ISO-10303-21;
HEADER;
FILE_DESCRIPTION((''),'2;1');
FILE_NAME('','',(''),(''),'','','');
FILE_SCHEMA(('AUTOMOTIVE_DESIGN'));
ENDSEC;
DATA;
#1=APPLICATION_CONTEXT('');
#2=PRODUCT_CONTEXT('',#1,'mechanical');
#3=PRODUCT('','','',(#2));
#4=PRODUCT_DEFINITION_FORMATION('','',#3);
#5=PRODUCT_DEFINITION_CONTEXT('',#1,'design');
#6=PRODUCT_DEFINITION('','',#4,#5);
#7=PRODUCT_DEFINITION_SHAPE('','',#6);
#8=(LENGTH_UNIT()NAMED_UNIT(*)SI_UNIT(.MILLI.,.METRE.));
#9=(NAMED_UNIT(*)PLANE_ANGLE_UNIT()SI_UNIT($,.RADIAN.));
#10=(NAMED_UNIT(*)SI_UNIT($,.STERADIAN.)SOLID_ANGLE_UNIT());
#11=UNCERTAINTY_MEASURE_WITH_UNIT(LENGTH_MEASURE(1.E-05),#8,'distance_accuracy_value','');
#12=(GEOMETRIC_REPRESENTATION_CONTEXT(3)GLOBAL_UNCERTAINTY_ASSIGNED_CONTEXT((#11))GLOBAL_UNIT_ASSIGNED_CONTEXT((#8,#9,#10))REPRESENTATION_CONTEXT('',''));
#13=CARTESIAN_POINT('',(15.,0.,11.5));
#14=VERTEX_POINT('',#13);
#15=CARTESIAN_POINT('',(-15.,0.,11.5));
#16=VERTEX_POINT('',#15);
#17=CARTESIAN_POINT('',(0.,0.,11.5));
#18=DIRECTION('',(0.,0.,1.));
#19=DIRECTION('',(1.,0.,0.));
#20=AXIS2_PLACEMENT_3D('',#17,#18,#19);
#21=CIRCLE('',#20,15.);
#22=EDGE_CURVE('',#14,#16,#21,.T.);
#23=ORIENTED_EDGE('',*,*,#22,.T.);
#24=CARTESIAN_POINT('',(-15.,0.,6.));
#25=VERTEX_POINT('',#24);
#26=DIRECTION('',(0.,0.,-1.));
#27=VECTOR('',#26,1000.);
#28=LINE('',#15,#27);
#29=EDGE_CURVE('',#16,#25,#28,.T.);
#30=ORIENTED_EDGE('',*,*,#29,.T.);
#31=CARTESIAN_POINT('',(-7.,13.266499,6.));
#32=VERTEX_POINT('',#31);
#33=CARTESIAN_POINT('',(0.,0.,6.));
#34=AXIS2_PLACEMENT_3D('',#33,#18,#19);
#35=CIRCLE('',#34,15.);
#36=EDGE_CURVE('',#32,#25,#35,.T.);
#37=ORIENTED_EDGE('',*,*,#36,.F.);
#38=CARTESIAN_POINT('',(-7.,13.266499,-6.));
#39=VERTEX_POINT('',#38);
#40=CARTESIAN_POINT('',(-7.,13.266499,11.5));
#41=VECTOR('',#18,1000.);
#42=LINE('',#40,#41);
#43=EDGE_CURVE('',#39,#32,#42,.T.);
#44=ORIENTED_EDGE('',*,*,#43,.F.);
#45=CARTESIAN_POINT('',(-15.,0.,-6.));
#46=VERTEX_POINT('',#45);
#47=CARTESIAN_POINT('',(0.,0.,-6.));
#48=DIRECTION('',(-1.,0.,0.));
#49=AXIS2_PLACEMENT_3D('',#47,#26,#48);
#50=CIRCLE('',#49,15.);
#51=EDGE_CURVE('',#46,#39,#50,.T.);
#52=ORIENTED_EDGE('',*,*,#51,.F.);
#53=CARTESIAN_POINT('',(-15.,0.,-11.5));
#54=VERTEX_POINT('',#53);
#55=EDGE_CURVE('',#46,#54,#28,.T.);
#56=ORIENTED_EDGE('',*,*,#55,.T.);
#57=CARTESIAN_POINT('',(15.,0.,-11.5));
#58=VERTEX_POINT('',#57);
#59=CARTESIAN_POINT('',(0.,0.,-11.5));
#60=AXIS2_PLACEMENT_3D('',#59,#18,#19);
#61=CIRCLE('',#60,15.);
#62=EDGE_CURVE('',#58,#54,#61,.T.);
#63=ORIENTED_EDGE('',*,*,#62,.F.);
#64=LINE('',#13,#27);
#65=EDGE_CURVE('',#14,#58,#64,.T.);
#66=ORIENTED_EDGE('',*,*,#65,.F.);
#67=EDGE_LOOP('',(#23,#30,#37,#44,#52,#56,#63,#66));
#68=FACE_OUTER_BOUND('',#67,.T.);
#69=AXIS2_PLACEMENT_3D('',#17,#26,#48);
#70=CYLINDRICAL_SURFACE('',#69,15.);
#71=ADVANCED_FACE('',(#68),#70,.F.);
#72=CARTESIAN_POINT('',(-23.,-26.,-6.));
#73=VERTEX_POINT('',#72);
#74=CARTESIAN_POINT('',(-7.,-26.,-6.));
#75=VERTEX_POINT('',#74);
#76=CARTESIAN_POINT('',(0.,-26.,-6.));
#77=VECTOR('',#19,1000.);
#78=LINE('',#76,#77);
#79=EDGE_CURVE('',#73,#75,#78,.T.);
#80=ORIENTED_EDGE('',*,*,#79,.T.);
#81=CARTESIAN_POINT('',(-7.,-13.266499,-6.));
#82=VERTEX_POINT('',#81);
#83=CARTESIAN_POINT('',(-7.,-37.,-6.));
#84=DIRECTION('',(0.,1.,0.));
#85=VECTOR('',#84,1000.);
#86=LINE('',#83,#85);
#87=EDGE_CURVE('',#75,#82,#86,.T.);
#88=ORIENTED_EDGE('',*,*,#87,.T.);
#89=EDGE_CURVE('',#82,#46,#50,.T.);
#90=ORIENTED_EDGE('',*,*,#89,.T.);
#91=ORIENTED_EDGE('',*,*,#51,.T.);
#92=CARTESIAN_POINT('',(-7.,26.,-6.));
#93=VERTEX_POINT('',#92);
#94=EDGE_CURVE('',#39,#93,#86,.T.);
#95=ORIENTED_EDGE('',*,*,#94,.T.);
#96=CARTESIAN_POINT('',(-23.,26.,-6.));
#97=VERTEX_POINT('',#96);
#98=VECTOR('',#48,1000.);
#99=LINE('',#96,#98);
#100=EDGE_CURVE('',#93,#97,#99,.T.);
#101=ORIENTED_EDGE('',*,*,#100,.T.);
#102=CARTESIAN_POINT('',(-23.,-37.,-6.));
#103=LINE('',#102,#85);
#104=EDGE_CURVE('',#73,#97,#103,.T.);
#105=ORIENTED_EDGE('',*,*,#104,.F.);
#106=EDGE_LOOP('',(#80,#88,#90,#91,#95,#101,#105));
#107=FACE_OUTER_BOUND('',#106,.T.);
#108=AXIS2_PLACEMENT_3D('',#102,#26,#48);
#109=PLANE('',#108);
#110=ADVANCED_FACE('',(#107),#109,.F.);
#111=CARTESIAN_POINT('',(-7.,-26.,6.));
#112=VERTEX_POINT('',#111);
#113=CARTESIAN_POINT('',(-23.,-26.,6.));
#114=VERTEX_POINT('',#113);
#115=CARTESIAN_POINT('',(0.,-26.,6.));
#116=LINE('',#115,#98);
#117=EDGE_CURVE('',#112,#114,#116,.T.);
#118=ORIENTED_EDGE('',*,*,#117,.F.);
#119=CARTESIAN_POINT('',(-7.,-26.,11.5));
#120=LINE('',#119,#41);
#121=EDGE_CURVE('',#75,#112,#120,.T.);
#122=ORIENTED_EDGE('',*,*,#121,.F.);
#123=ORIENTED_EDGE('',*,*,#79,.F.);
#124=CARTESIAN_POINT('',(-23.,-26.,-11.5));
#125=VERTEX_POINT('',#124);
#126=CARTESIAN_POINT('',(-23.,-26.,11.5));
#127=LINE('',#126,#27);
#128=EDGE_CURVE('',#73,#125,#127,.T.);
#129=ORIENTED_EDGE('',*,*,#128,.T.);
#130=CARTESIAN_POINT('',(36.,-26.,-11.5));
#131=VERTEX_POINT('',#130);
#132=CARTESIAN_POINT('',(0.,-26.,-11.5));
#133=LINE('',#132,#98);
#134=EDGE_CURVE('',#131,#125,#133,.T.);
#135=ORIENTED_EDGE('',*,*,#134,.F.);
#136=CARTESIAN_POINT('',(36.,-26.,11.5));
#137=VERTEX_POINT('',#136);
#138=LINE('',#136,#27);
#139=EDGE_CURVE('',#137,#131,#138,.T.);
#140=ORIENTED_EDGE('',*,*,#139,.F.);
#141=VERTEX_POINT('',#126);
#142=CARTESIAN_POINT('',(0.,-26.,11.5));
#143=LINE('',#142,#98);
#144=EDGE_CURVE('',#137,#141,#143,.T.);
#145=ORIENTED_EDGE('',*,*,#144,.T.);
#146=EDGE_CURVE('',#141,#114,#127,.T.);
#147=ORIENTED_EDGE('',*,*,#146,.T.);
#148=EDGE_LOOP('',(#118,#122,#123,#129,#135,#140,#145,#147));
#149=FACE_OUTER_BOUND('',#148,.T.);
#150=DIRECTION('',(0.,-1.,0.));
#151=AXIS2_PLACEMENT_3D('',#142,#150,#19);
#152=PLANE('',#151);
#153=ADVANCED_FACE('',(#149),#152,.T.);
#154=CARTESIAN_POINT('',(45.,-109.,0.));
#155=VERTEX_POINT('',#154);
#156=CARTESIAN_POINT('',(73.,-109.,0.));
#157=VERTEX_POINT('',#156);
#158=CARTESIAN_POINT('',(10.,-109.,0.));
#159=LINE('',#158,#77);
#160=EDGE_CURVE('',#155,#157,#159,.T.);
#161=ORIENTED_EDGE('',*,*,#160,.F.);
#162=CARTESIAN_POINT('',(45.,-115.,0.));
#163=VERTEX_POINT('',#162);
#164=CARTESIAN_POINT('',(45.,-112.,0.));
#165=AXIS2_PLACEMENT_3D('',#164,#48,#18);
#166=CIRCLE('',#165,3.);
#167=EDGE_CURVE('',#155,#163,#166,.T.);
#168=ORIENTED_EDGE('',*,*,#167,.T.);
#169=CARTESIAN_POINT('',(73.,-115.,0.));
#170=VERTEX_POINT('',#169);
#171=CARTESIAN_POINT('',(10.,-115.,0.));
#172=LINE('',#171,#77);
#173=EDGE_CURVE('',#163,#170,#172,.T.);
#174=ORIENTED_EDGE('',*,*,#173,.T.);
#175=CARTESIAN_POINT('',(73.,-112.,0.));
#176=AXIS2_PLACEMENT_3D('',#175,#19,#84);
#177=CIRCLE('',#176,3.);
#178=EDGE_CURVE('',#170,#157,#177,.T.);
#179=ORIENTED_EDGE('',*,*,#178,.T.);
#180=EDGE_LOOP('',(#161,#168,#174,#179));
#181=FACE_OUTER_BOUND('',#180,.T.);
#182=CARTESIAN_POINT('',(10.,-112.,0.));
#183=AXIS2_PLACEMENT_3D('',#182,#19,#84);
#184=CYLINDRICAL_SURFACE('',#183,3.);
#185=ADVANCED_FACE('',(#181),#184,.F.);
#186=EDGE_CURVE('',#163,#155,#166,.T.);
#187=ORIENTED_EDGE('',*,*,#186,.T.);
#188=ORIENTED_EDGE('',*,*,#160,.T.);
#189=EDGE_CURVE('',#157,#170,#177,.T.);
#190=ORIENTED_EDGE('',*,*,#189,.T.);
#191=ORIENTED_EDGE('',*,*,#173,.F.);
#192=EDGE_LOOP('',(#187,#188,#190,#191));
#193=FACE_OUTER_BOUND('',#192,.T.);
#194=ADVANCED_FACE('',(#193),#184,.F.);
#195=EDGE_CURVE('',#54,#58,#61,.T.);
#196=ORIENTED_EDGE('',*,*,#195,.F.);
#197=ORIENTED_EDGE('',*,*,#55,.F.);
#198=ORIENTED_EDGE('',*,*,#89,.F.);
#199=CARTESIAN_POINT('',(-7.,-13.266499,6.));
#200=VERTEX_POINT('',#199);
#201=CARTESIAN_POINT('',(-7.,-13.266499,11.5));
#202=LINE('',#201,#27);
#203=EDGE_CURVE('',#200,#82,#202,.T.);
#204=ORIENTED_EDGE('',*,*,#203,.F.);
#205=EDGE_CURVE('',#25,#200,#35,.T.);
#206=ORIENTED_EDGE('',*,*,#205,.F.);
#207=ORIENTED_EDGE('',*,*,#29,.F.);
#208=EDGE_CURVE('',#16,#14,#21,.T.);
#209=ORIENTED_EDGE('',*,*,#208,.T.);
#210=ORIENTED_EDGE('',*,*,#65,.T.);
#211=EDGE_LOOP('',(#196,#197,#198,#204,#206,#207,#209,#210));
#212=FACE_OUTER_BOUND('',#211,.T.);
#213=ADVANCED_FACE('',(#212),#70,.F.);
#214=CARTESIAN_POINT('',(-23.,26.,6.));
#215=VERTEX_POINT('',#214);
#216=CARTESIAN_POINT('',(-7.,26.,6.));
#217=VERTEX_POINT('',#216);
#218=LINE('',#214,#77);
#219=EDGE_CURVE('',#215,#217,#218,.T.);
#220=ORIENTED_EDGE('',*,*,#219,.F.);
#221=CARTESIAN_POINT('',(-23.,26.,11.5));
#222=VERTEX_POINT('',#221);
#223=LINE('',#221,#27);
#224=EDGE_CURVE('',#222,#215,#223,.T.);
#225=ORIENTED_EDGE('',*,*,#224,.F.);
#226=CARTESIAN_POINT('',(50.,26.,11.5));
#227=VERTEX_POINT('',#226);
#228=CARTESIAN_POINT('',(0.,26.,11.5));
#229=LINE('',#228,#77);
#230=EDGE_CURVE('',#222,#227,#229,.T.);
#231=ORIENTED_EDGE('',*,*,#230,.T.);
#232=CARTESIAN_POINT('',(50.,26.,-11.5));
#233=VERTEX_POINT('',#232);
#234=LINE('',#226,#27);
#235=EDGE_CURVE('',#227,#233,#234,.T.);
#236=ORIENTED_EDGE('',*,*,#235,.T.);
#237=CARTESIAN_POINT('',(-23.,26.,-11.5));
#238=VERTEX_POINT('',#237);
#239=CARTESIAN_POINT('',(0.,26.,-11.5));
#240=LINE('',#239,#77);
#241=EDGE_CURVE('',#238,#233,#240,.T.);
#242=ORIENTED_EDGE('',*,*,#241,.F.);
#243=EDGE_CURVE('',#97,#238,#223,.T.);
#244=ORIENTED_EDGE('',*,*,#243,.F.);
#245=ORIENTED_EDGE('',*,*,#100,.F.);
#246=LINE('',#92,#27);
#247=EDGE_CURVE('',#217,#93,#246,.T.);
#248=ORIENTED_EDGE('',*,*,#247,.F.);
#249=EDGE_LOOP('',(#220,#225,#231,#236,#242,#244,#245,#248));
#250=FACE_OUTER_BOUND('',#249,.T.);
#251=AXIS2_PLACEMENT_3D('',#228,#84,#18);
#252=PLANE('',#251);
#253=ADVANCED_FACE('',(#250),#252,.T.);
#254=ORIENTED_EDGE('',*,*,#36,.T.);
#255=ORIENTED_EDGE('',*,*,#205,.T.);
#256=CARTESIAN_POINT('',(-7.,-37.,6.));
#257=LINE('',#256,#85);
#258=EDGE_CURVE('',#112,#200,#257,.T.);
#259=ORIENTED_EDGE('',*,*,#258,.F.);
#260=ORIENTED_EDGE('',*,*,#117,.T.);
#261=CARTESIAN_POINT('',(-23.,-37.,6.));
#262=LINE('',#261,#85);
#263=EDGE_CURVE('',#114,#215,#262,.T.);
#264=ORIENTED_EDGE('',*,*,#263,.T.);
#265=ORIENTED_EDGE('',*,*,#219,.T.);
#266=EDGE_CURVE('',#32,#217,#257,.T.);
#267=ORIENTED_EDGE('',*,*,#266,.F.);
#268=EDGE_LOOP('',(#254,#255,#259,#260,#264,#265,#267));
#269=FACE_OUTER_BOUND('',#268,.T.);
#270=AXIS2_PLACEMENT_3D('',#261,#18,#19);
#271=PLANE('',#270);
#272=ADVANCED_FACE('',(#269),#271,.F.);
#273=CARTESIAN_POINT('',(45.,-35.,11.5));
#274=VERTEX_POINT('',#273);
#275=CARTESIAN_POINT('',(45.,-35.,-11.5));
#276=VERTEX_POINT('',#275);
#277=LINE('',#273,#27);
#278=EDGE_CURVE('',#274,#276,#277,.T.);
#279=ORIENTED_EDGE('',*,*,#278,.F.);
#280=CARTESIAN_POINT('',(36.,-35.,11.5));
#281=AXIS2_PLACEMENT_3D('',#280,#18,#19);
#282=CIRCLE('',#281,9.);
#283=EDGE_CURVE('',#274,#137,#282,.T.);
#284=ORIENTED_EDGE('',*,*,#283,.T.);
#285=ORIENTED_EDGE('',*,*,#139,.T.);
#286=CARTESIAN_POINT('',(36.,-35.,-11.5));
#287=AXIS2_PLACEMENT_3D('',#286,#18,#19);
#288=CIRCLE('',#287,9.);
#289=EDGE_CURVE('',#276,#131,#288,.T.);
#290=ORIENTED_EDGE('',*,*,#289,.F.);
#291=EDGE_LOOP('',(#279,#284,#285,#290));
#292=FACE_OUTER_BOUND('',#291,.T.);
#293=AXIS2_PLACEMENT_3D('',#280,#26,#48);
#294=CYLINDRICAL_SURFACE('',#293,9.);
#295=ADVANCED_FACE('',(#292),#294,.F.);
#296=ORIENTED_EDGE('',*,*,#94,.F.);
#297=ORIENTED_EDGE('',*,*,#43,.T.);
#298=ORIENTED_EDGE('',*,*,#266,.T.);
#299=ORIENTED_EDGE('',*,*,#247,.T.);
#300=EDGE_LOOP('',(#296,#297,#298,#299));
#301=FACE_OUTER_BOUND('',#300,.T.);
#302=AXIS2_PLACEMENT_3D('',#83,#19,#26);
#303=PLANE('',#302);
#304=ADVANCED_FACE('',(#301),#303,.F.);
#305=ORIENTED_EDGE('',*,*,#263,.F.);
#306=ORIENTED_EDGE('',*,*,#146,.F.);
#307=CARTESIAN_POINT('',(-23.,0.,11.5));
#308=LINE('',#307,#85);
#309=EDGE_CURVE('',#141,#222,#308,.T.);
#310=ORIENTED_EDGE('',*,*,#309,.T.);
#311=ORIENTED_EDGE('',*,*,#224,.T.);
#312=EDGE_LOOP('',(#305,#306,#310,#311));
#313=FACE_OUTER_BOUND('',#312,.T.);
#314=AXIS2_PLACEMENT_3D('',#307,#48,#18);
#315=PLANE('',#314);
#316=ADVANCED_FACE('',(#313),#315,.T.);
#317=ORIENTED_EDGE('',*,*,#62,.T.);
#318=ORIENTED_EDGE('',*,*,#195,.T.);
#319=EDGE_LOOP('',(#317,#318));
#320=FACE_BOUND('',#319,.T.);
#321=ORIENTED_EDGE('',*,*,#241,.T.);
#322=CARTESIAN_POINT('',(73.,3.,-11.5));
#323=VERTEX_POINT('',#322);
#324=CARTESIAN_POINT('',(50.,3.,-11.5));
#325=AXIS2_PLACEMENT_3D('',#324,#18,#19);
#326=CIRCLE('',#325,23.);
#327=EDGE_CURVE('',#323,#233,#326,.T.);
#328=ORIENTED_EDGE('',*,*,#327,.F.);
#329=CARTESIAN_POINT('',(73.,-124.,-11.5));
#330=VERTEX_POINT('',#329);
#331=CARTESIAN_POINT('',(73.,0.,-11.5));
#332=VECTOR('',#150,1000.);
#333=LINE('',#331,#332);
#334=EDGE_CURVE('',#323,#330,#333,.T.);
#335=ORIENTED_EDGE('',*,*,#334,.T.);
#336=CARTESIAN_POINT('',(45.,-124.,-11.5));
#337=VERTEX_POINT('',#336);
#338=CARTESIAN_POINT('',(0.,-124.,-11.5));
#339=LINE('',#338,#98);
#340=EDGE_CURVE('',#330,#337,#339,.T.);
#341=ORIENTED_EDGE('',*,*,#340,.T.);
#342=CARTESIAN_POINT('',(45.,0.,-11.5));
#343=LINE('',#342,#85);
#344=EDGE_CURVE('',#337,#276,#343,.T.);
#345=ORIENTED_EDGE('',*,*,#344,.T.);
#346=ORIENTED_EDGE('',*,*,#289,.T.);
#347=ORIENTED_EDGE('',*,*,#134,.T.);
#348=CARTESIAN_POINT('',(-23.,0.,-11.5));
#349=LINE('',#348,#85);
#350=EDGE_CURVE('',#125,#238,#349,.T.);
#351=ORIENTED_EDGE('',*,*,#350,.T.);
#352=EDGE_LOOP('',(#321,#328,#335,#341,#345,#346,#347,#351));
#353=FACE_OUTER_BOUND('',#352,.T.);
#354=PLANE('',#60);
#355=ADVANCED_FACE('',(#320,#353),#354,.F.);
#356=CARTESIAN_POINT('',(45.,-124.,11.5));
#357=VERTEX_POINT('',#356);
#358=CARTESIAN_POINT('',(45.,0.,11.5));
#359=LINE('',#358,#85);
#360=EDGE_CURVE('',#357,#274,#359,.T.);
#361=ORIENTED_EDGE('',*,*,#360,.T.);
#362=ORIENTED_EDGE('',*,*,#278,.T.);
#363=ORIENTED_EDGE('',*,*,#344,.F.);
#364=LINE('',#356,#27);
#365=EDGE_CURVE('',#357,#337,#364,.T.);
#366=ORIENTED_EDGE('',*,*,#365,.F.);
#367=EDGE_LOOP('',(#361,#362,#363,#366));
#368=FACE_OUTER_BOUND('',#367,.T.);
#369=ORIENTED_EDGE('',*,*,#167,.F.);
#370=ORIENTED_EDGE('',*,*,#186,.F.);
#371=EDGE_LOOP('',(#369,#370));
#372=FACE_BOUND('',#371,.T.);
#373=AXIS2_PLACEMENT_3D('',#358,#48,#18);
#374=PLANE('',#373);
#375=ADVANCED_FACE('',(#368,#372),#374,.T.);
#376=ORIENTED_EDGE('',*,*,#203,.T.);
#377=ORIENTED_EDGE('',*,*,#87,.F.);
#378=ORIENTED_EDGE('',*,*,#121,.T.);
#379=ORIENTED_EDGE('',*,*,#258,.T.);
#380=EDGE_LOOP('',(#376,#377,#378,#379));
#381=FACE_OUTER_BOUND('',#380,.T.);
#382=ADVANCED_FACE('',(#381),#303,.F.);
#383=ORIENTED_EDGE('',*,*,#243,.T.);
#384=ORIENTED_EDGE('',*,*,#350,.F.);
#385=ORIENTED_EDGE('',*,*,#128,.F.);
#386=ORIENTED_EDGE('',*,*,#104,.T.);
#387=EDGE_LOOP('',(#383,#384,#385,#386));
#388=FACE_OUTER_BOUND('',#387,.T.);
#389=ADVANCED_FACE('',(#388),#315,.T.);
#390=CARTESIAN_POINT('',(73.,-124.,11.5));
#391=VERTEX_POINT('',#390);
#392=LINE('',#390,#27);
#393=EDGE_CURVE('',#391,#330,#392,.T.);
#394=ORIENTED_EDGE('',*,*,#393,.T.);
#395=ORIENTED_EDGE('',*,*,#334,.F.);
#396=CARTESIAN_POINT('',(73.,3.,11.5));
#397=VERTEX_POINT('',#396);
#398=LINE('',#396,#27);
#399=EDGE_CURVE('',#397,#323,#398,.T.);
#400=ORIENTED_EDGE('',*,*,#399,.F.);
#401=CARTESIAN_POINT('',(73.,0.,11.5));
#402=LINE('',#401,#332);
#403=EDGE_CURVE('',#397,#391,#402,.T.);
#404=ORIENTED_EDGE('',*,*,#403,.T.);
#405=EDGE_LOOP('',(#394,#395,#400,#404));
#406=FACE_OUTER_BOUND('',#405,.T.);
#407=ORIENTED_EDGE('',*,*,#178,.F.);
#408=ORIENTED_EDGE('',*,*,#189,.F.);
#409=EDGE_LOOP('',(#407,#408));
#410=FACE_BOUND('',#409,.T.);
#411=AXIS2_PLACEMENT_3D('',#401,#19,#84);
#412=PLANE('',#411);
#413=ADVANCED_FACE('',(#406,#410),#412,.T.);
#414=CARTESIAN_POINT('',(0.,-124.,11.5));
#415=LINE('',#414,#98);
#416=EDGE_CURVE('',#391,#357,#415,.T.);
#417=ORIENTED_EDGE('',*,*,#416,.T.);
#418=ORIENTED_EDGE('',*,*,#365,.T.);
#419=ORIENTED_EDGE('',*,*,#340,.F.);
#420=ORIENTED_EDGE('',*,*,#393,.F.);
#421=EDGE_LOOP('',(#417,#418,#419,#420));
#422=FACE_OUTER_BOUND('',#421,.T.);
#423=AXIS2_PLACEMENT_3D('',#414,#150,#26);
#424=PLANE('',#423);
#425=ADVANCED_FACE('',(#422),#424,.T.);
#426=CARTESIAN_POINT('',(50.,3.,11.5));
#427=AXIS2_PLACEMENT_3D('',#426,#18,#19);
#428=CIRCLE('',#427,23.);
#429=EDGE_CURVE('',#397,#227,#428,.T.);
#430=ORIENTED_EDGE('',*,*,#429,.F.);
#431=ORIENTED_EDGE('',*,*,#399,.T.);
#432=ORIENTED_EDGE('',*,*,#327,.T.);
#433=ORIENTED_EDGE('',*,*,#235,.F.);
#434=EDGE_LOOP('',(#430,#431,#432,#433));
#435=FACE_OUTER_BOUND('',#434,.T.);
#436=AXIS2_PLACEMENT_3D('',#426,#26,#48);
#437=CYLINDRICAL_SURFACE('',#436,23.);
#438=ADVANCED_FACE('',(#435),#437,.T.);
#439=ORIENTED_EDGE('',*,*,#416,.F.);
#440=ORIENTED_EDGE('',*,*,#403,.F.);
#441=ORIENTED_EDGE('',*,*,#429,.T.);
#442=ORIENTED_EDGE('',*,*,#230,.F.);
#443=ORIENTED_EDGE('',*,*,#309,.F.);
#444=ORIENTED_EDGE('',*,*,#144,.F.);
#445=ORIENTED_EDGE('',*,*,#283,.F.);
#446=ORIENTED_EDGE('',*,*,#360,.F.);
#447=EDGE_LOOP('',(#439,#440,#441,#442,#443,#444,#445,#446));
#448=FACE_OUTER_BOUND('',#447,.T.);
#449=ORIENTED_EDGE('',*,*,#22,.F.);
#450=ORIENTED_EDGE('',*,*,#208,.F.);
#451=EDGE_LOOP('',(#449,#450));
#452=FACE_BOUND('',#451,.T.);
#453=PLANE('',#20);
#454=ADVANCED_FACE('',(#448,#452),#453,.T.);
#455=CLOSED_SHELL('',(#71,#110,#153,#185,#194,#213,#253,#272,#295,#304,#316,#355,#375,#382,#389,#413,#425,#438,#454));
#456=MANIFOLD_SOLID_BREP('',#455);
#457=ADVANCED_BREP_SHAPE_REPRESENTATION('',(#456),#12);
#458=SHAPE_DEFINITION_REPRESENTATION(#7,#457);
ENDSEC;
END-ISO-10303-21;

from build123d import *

# Parameters (mm, degrees)
BRACKET_PROFILE_SKETCH_R = 15
L_BRACKET_BODY_DEPTH     = 11.5
SLOT_CUT_SKETCH_W        = 16
SLOT_CUT_SKETCH_H        = 12
SLOT_CUT_DEPTH           = 63
END_HOLE_SKETCH_R        = 3
END_HOLE_DEPTH           = 63


with BuildPart() as part:
    # Bracket Profile Sketch → L-Bracket Body (new, symmetric)
    with BuildSketch(Plane.XY):
        with BuildLine():
            Line((73, 3), (73, -124))
            Line((73, -124), (45, -124))
            Line((45, -124), (45, -35))
            ThreePointArc((45, -35), (42.363961031, -28.636038969), (36, -26))
            Line((36, -26), (-23, -26))
            Line((-23, -26), (-23, 26))
            Line((-23, 26), (50, 26))
            ThreePointArc((50, 26), (66.263455967, 19.263455967), (73, 3))
        make_face()
        Circle(BRACKET_PROFILE_SKETCH_R, mode=Mode.SUBTRACT)
    extrude(amount=L_BRACKET_BODY_DEPTH, both=True)

    # Slot Cut Sketch → Slot Cut (cut)
    with BuildSketch(Plane(origin=(0, 26, 0), x_dir=(1, 0, 0), z_dir=(0, 1, 0))):
        with Locations((-15, 0)):
            Rectangle(SLOT_CUT_SKETCH_W, SLOT_CUT_SKETCH_H)
    extrude(amount=-SLOT_CUT_DEPTH, mode=Mode.SUBTRACT)

    # End Hole Sketch → End Hole (cut)
    with BuildSketch(Plane(origin=(73, 0, 0), x_dir=(0, 0, -1), z_dir=(1, 0, 0))):
        with Locations(Location((0, -112, 0), (0, 0, 90))):
            Circle(END_HOLE_SKETCH_R)
    extrude(amount=-END_HOLE_DEPTH, mode=Mode.SUBTRACT)


solid = part.part
